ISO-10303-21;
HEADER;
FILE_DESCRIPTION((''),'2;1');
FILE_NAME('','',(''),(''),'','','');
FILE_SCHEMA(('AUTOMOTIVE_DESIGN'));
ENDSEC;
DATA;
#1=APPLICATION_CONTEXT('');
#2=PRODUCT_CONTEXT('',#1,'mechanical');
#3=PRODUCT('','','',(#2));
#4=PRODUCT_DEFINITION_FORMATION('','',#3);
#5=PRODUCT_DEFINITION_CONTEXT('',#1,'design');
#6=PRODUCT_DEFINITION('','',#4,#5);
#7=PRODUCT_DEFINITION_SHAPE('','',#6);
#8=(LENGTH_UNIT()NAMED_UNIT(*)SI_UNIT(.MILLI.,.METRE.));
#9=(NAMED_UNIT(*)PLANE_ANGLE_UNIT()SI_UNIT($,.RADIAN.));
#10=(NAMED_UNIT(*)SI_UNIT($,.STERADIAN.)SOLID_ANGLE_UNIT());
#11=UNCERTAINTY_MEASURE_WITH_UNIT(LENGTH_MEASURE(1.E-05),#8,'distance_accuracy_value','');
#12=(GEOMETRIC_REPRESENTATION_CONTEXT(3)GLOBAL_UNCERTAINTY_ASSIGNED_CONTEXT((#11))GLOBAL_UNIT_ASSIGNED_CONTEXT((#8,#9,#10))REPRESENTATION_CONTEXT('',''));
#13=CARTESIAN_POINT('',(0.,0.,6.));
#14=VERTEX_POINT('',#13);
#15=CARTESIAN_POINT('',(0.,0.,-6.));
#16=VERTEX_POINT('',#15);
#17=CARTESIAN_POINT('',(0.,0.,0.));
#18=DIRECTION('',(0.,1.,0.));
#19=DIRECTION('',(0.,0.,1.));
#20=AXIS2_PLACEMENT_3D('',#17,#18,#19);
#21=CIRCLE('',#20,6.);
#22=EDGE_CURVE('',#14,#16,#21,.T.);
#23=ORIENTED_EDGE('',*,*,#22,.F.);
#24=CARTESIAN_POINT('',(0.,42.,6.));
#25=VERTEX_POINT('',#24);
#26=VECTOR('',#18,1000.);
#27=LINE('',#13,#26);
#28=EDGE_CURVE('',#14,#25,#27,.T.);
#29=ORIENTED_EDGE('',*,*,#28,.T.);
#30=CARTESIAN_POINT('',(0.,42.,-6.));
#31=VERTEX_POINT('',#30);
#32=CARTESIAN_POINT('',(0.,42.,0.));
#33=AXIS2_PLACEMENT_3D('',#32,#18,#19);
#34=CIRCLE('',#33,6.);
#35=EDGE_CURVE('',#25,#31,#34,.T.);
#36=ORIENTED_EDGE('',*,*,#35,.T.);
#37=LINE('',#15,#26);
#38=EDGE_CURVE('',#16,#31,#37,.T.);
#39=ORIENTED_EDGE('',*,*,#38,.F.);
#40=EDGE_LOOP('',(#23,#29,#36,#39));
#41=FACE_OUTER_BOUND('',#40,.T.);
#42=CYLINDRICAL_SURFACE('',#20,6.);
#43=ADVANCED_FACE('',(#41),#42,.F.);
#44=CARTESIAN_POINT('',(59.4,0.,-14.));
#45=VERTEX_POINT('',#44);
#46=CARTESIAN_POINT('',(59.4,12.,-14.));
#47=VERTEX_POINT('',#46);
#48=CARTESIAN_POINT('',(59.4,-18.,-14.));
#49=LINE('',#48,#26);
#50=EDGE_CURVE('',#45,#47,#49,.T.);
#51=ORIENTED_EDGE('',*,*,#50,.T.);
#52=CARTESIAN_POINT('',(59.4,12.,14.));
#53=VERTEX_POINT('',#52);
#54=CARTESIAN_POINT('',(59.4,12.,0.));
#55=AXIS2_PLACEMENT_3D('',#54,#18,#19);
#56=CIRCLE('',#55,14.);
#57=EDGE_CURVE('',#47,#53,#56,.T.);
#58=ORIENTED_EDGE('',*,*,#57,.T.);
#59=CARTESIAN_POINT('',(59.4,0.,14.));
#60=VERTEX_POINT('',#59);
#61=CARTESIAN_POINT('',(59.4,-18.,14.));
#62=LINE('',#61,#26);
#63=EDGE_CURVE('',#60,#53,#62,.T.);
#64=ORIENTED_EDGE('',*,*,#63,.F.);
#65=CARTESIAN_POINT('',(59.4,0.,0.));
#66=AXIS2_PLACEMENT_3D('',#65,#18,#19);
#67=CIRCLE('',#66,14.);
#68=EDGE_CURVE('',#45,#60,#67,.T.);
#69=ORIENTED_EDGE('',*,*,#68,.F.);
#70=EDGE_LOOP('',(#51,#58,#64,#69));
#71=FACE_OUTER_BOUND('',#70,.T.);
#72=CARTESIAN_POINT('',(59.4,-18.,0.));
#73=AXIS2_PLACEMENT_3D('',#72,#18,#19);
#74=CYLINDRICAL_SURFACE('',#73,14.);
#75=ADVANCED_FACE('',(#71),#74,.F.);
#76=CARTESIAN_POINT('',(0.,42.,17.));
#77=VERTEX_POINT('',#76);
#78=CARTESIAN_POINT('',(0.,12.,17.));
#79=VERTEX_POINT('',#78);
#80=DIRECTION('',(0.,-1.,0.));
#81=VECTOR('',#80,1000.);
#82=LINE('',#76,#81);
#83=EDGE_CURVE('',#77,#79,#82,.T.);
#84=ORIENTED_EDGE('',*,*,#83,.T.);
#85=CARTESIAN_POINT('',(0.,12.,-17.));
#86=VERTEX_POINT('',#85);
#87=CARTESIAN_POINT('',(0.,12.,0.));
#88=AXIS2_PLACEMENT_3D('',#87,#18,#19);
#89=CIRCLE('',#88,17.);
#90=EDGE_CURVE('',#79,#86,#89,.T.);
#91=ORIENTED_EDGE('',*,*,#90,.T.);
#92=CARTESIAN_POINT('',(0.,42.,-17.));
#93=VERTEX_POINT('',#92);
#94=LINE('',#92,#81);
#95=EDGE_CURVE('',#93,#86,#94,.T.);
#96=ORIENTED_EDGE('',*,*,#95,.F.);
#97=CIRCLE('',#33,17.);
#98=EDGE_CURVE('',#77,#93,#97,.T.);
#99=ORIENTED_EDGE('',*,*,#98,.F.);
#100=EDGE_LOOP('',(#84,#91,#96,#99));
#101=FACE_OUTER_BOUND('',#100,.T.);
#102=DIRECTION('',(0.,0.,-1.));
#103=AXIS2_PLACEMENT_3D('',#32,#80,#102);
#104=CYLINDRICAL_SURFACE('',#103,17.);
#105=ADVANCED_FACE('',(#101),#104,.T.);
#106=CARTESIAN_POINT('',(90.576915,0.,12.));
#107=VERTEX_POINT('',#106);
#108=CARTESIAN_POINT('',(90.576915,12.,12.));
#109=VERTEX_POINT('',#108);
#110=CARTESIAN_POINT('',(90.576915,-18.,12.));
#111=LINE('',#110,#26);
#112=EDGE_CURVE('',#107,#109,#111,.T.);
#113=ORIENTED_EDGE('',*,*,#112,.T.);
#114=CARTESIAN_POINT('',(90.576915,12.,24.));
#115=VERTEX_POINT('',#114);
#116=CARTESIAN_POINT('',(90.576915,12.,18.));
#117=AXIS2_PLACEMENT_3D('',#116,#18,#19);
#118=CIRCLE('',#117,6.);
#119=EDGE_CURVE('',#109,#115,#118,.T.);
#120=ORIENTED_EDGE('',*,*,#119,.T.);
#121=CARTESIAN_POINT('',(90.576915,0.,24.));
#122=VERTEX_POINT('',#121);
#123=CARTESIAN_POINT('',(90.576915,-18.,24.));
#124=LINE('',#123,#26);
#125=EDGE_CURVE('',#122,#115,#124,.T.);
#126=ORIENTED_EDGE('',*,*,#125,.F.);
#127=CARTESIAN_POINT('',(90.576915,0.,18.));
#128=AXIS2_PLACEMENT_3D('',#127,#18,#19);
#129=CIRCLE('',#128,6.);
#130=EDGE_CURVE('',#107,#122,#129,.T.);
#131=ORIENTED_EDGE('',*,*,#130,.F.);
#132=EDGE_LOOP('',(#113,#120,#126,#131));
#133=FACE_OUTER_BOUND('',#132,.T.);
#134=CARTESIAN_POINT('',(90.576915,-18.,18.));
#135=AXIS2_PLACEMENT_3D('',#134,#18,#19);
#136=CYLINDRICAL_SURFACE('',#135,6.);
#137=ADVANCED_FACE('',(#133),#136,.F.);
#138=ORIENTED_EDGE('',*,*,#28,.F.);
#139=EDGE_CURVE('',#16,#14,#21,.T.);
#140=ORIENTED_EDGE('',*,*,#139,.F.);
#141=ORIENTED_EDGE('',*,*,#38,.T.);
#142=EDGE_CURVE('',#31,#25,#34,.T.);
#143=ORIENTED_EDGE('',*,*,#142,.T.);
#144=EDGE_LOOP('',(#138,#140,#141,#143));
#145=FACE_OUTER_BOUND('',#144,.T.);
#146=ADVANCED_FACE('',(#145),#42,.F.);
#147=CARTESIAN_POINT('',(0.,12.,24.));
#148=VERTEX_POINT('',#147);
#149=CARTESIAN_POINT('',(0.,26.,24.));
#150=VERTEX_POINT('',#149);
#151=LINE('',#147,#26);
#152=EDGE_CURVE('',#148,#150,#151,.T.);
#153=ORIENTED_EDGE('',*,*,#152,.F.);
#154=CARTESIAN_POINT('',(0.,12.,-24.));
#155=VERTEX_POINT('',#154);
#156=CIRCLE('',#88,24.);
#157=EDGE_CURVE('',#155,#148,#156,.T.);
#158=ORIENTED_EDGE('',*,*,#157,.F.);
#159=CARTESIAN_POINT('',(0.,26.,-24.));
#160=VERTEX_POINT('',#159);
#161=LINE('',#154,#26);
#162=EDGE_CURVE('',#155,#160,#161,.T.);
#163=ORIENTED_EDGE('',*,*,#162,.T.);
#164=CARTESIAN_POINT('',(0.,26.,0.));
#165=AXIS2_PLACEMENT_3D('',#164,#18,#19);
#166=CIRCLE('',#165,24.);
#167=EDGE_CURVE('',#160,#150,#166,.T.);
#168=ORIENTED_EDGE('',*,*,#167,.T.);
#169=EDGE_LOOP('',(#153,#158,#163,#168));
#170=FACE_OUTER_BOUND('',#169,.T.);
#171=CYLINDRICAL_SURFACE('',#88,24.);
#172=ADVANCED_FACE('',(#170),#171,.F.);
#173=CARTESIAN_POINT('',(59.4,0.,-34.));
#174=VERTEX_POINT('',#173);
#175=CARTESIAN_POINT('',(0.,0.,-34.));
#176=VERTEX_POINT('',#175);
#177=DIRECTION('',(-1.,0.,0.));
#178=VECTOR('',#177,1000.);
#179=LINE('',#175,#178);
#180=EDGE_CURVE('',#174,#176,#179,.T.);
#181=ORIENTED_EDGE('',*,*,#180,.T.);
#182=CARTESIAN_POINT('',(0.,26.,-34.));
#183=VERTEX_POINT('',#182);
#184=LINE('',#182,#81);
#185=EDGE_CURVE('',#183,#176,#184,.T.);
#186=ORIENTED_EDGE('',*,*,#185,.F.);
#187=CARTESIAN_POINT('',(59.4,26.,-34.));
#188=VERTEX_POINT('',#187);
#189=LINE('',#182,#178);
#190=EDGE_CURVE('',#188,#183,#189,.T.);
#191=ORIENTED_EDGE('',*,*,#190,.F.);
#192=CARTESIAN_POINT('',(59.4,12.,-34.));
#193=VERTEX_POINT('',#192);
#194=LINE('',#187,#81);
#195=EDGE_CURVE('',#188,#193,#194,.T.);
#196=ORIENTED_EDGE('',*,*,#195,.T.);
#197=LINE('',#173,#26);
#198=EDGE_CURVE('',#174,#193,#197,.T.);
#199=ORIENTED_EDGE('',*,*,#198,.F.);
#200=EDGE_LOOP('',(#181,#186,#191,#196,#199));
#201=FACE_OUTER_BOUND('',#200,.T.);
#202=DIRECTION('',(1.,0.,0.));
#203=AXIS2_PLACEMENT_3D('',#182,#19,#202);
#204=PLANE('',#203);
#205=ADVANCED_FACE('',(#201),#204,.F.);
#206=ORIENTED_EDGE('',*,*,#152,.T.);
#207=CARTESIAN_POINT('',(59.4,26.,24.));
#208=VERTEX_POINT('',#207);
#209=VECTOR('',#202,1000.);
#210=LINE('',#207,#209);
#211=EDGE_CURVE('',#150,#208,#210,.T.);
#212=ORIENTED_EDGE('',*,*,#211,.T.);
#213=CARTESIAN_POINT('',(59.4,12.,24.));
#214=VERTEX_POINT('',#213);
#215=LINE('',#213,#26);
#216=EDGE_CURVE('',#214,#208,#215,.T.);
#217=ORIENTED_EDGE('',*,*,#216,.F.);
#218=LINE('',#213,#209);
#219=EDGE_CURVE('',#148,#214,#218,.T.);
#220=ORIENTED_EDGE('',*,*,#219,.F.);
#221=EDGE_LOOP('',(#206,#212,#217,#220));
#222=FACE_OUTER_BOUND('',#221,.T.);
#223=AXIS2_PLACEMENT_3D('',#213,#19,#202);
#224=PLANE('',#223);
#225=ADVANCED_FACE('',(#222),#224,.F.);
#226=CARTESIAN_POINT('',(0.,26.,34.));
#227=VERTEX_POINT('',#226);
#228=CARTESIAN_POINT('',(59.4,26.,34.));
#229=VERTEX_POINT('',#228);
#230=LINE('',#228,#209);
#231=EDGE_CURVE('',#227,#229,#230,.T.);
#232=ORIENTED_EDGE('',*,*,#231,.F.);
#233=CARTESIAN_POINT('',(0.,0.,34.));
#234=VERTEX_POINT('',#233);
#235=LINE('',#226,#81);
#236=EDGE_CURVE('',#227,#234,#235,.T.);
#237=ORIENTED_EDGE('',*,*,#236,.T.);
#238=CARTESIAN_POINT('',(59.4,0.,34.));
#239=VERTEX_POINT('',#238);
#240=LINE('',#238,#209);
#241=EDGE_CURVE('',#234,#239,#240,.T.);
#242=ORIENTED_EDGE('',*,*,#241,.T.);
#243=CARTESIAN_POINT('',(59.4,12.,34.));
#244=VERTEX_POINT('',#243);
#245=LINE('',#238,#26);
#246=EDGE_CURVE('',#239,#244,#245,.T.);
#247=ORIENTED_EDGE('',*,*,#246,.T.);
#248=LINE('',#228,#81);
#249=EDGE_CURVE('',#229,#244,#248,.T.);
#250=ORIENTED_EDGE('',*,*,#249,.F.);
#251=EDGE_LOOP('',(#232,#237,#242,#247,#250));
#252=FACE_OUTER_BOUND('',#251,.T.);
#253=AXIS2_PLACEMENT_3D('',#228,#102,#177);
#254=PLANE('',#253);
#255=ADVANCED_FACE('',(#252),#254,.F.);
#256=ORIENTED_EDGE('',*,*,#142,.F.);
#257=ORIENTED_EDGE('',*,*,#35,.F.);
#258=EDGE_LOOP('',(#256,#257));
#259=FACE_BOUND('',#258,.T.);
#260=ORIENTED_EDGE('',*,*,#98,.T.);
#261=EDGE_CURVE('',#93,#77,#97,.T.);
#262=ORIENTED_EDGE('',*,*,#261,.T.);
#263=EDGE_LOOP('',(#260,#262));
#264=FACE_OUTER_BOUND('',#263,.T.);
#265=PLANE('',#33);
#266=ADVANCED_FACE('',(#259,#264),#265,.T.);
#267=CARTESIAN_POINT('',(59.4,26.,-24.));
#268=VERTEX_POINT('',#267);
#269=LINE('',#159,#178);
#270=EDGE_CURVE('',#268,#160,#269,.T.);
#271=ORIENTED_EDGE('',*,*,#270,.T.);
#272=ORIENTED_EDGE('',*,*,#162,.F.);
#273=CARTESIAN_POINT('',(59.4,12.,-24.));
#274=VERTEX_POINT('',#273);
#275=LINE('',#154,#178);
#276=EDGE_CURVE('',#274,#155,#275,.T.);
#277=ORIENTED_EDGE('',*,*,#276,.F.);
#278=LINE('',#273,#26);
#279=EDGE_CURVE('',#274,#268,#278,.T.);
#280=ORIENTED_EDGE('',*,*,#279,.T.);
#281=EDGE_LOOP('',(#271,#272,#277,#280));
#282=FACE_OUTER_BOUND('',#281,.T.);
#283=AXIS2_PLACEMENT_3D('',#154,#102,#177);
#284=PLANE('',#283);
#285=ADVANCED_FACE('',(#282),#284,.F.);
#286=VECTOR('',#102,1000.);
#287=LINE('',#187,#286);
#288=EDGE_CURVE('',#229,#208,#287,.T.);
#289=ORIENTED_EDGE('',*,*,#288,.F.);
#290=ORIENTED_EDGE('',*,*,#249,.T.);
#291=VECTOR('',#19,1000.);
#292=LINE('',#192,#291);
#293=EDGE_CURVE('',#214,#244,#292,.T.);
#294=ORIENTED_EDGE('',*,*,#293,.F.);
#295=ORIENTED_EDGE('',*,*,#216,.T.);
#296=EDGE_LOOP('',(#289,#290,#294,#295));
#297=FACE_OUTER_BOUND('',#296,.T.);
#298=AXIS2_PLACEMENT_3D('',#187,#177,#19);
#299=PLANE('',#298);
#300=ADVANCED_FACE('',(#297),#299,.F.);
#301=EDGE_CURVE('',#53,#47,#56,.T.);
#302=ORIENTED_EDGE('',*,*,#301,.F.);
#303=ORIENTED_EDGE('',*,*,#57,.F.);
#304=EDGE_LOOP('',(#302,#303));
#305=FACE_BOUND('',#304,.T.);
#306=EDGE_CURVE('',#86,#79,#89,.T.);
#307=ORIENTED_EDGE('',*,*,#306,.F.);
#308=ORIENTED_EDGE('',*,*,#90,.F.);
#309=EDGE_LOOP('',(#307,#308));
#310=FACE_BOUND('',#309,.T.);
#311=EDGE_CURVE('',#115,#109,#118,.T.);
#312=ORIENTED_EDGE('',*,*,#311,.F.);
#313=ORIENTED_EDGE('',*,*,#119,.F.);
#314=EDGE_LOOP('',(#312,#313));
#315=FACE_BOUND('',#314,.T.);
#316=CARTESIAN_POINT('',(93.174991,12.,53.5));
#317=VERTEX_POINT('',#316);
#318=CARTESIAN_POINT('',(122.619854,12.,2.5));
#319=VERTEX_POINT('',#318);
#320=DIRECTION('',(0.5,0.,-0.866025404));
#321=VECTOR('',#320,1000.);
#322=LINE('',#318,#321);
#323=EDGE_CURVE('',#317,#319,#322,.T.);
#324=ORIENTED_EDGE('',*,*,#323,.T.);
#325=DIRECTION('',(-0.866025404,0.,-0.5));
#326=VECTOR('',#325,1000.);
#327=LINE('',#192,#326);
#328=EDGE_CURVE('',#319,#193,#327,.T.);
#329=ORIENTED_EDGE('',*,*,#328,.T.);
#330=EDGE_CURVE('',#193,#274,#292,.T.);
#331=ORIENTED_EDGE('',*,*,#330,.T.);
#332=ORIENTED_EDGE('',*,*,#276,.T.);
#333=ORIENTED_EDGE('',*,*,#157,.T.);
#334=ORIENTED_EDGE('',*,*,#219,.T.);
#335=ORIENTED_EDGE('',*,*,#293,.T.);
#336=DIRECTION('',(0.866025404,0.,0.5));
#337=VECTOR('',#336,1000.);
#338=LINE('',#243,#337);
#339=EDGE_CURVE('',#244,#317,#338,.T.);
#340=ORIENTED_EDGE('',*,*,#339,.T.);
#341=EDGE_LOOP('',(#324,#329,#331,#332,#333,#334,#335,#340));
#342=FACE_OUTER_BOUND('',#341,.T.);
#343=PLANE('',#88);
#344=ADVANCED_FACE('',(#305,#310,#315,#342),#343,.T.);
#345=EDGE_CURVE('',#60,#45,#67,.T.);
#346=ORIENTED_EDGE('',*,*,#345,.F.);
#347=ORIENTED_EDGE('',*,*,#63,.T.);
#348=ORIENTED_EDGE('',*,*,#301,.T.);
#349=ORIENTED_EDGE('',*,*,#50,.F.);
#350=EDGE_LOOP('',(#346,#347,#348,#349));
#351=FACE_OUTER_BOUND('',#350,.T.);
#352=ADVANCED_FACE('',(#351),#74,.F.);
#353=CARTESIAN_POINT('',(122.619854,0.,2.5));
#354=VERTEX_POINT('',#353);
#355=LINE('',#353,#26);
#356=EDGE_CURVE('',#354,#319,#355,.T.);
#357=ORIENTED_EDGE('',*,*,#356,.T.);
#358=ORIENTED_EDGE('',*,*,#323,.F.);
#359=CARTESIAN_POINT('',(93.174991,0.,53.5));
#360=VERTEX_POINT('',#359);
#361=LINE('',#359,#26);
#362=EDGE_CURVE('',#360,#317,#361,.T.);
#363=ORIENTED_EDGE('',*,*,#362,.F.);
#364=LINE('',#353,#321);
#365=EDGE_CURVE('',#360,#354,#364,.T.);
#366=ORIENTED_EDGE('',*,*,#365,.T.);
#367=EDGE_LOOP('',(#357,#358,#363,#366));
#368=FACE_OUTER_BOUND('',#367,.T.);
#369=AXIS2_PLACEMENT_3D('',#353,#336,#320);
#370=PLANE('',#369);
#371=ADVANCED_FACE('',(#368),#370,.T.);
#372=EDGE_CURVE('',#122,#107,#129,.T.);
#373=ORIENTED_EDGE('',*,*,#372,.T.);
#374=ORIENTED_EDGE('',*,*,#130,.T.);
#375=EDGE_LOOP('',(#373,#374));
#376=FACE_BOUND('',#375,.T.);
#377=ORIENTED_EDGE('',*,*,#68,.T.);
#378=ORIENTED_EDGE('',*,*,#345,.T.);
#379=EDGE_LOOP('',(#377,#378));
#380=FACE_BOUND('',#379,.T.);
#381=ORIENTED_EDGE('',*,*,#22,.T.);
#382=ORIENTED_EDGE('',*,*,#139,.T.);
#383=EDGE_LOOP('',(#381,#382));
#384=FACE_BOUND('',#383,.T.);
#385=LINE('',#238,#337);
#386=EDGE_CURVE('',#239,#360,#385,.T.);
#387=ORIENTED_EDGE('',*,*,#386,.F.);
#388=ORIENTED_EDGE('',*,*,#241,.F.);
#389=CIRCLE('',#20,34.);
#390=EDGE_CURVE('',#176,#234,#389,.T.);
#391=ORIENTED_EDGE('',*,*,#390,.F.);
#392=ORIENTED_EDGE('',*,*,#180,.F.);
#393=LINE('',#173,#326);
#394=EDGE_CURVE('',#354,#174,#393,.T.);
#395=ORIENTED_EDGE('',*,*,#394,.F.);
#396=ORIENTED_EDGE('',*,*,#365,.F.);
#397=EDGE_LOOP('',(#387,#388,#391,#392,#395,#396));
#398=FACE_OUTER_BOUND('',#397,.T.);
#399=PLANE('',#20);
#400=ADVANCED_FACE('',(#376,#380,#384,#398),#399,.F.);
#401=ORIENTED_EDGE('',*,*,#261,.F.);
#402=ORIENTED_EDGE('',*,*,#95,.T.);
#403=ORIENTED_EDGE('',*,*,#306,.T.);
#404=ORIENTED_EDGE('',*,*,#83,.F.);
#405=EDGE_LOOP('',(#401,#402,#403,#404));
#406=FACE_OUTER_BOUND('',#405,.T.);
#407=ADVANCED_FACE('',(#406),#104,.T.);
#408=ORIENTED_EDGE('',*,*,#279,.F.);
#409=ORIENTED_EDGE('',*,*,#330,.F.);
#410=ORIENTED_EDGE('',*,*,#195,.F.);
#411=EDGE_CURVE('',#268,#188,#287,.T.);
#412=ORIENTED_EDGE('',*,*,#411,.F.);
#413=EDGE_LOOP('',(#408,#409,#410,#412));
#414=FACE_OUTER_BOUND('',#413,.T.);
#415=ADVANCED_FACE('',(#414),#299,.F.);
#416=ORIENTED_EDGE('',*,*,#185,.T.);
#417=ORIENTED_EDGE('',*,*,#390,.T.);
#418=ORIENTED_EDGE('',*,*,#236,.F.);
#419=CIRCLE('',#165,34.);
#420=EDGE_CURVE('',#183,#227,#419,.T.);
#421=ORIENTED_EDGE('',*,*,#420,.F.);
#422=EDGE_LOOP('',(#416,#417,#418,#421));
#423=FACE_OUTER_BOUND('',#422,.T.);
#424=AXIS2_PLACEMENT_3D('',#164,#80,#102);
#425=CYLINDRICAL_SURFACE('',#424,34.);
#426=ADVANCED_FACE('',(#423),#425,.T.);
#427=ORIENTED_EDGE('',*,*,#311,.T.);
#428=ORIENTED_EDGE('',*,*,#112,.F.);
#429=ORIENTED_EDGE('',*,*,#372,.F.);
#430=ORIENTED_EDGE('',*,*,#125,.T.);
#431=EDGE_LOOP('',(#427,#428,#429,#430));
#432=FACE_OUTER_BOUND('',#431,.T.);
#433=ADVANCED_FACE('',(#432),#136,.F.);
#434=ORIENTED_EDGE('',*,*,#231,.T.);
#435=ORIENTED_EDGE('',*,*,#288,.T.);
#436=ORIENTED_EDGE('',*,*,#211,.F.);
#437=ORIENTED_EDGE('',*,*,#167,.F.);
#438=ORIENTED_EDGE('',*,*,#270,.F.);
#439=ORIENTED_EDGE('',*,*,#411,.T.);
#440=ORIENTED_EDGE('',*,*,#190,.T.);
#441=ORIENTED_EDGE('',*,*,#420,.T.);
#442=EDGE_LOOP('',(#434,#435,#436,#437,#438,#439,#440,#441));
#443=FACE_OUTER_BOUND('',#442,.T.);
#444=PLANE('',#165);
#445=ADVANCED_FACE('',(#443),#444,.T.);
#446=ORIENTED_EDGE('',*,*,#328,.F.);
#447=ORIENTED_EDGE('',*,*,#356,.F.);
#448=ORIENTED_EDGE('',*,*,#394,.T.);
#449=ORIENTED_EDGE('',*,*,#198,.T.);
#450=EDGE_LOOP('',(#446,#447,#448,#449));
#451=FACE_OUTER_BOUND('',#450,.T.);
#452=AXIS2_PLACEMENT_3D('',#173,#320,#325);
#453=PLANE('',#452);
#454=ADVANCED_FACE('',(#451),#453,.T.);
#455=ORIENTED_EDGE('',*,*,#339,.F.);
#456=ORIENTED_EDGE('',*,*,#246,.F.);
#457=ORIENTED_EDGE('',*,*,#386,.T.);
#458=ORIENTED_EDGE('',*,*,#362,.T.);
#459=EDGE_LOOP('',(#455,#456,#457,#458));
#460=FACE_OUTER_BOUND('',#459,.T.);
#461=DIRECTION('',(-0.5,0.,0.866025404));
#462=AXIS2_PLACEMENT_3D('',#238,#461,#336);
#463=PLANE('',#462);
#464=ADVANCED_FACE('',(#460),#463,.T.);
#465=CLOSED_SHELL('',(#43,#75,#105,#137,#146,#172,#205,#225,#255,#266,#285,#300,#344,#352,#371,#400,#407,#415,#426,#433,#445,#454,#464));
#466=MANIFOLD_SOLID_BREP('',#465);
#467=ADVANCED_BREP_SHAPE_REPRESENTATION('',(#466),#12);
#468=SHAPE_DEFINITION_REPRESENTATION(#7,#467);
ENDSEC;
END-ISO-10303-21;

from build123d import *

# Parameters (mm, degrees)
BASE_PLATE_DEPTH          = 26
U_POCKET_14_DEEP_DEPTH    = 14
ANGLED_TAB_30DEG_DEPTH    = 12
BOSS_CIRCLE_SKETCH_R      = 17
BOSS_34_DEPTH             = 30
BOSS_BORE_SKETCH_R        = 6
BOSS_BORE_12_DEPTH        = 141.220821249
TAB_HOLES_SKETCH_R        = 14
TAB_HOLES_SKETCH_R_2      = 6
TAB_HOLES_28_AND_12_DEPTH = 30


with BuildPart() as part:
    # Base Profile Sketch → Base Plate (new body)
    with BuildSketch(Plane(origin=(0, 0, 0), x_dir=(1, 0, 0), z_dir=(0, 1, 0))):
        with BuildLine():
            Line((0, 34), (59.4, 34))
            Line((59.4, 34), (59.4, -34))
            Line((59.4, -34), (0, -34))
            ThreePointArc((0, -34), (-34, 0), (0, 34))
        make_face()
    extrude(amount=BASE_PLATE_DEPTH)

    # Pocket Profile Sketch → U Pocket 14 Deep (cut)
    with BuildSketch(Plane(origin=(0, 26, 0), x_dir=(1, 0, 0), z_dir=(0, 1, 0))):
        with BuildLine():
            Line((0, 24), (59.4, 24))
            Line((59.4, 24), (59.4, -24))
            Line((59.4, -24), (0, -24))
            ThreePointArc((0, -24), (-24, 0), (0, 24))
        make_face()
    extrude(amount=-U_POCKET_14_DEEP_DEPTH, mode=Mode.SUBTRACT)

    # Angled Tab Sketch → Angled Tab 30deg (add)
    with BuildSketch(Plane(origin=(0, 12, 0), x_dir=(1, 0, 0), z_dir=(0, 1, 0))):
        Polygon((59.4, 34), (122.619854476, -2.5), (93.174990748, -53.5), (59.4, -34), align=None)
    extrude(amount=-ANGLED_TAB_30DEG_DEPTH)

    # Boss Circle Sketch → Boss Ø34 (add)
    with BuildSketch(Plane(origin=(0, 12, 0), x_dir=(1, 0, 0), z_dir=(0, 1, 0))):
        with Locations(Location((0, 0, 0), (0, 0, 270))):
            Circle(BOSS_CIRCLE_SKETCH_R)
    extrude(amount=BOSS_34_DEPTH)

    # Boss Bore Sketch → Boss Bore Ø12 (cut, through all)
    with BuildSketch(Plane(origin=(0, 42, 0), x_dir=(1, 0, 0), z_dir=(0, 1, 0))):
        with Locations(Location((0, 0, 0), (0, 0, 270))):
            Circle(BOSS_BORE_SKETCH_R)
    extrude(amount=-BOSS_BORE_12_DEPTH, mode=Mode.SUBTRACT)

    # Tab Holes Sketch → Tab Holes Ø28 and Ø12 (cut)
    with BuildSketch(Plane(origin=(0, 12, 0), x_dir=(1, 0, 0), z_dir=(0, 1, 0))):
        with Locations(Location((59.4, 0, 0), (0, 0, 270))):
            Circle(TAB_HOLES_SKETCH_R)
        with Locations(Location((90.576914536, -18, 0), (0, 0, 270))):
            Circle(TAB_HOLES_SKETCH_R_2)
    extrude(amount=-TAB_HOLES_28_AND_12_DEPTH, mode=Mode.SUBTRACT)


solid = part.part
